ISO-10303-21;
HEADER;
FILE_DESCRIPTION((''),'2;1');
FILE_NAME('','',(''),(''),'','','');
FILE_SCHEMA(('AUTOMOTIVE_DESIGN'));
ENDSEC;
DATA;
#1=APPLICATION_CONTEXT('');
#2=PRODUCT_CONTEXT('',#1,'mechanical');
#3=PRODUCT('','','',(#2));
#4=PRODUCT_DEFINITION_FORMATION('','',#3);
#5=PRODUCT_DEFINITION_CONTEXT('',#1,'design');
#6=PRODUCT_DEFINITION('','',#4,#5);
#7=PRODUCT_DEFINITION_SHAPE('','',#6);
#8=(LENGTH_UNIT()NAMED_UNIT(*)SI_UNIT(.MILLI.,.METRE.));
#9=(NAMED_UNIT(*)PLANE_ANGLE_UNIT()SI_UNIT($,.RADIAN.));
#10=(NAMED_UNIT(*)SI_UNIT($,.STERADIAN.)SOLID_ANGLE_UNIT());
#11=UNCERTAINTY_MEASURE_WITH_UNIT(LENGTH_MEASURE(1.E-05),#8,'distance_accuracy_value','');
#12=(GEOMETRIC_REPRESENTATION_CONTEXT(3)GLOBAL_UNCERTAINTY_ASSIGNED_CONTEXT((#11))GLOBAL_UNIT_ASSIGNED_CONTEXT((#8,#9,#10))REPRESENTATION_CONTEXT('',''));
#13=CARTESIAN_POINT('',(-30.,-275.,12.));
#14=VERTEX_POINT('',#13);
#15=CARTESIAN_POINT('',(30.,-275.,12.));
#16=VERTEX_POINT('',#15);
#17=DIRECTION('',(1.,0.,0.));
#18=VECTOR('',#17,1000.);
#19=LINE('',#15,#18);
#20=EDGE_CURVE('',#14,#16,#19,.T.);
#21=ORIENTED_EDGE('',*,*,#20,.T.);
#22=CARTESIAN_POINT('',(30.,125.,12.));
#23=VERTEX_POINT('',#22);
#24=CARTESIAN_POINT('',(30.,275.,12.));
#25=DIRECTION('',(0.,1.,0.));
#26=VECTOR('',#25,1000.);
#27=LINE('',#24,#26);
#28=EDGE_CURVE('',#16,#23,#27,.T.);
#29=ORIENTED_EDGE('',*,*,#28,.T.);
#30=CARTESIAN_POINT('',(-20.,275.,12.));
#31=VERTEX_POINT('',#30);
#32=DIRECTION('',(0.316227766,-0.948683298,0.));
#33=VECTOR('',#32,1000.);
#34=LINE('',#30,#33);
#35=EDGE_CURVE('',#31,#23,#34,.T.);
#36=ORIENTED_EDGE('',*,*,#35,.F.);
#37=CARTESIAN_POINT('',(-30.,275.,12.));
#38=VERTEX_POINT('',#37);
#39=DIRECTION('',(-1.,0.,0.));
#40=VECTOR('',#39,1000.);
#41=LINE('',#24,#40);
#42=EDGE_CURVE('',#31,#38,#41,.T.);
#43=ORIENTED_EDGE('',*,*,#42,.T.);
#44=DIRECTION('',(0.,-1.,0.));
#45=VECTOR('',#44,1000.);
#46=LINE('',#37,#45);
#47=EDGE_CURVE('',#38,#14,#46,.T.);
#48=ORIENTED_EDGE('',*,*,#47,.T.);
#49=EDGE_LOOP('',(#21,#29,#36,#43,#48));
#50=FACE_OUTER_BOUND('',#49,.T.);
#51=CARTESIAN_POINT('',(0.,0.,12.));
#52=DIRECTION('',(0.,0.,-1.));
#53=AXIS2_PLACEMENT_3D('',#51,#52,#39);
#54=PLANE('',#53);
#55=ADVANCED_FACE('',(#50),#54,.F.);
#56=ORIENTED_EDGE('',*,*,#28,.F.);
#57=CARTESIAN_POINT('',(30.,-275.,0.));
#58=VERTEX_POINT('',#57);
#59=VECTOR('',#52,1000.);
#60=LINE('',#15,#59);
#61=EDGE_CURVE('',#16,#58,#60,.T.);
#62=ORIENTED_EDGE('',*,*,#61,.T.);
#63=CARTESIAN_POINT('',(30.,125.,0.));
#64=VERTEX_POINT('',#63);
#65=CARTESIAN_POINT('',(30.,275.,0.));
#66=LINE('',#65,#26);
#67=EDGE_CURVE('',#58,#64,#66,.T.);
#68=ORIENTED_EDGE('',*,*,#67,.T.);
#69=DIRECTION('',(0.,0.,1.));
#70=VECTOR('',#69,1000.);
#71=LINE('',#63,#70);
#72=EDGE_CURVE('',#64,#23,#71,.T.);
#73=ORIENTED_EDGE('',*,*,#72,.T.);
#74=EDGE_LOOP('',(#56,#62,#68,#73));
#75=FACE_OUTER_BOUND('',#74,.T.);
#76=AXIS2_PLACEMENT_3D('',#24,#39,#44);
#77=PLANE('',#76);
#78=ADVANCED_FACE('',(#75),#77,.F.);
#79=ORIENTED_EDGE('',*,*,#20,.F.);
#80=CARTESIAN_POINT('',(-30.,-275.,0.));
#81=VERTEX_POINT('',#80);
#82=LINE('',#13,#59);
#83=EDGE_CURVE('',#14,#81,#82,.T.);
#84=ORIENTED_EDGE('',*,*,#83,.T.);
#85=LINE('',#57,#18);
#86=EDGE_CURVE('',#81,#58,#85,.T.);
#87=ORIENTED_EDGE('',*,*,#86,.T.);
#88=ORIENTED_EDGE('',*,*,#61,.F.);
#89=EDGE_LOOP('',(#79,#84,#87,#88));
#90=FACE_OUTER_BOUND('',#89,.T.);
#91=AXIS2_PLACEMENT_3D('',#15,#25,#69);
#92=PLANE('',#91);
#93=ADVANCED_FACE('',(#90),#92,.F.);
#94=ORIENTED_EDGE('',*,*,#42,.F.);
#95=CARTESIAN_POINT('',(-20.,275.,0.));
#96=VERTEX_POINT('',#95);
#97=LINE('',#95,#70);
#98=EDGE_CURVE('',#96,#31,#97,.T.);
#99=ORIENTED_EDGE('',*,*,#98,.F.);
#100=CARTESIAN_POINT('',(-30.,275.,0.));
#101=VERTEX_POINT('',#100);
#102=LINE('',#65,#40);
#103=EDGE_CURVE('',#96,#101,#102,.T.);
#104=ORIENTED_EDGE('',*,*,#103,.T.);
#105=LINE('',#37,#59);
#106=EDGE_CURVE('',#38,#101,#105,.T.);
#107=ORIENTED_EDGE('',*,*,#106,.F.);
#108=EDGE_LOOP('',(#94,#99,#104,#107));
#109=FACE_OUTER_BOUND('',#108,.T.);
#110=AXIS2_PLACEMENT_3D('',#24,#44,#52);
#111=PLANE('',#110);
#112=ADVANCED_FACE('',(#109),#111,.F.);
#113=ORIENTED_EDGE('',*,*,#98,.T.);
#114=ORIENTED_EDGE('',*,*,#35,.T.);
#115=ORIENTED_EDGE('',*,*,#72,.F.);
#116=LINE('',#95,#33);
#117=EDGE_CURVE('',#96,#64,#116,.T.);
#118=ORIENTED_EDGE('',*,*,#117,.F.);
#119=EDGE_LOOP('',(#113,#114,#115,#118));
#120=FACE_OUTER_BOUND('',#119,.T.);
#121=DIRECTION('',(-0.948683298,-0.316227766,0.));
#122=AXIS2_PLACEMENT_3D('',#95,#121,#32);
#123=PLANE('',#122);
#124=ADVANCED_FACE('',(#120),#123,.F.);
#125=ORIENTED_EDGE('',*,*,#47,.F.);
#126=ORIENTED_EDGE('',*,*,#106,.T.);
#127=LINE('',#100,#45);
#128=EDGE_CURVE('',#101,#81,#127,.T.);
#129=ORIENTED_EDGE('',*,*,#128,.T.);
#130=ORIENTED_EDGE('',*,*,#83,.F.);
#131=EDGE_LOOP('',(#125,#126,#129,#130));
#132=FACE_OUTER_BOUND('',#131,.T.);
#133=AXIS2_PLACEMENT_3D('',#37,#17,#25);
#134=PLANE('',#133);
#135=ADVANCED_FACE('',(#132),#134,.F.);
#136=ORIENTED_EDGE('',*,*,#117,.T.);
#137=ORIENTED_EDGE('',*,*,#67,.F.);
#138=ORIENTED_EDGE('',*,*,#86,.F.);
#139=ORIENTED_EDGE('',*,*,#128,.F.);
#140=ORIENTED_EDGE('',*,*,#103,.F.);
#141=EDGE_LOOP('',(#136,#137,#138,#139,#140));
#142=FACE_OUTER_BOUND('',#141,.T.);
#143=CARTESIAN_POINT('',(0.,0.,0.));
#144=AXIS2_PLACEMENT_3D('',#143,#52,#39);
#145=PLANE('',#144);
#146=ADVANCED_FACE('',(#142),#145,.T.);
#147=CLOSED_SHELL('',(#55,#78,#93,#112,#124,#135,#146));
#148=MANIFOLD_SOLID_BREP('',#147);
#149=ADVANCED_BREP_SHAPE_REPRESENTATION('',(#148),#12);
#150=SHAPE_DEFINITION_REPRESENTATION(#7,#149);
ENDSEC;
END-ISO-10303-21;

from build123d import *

# Parameters (mm, degrees)
SKETCH_1_W          = 60
SKETCH_1_H          = 550
EXTRUDE_1_DEPTH     = 12
CUT_EXTRUDE_1_DEPTH = 12


with BuildPart() as part:
    # 草图1 → 凸台-拉伸1 (new body)
    with BuildSketch(Plane.XY):
        Rectangle(SKETCH_1_W, SKETCH_1_H)
    extrude(amount=EXTRUDE_1_DEPTH)

    # 草图2 → 切除-拉伸1 (cut)
    with BuildSketch(Plane.XY.offset(12)):
        Polygon((-20, 275), (30, 125), (30, 275), align=None)
    extrude(amount=-CUT_EXTRUDE_1_DEPTH, mode=Mode.SUBTRACT)


solid = part.part
